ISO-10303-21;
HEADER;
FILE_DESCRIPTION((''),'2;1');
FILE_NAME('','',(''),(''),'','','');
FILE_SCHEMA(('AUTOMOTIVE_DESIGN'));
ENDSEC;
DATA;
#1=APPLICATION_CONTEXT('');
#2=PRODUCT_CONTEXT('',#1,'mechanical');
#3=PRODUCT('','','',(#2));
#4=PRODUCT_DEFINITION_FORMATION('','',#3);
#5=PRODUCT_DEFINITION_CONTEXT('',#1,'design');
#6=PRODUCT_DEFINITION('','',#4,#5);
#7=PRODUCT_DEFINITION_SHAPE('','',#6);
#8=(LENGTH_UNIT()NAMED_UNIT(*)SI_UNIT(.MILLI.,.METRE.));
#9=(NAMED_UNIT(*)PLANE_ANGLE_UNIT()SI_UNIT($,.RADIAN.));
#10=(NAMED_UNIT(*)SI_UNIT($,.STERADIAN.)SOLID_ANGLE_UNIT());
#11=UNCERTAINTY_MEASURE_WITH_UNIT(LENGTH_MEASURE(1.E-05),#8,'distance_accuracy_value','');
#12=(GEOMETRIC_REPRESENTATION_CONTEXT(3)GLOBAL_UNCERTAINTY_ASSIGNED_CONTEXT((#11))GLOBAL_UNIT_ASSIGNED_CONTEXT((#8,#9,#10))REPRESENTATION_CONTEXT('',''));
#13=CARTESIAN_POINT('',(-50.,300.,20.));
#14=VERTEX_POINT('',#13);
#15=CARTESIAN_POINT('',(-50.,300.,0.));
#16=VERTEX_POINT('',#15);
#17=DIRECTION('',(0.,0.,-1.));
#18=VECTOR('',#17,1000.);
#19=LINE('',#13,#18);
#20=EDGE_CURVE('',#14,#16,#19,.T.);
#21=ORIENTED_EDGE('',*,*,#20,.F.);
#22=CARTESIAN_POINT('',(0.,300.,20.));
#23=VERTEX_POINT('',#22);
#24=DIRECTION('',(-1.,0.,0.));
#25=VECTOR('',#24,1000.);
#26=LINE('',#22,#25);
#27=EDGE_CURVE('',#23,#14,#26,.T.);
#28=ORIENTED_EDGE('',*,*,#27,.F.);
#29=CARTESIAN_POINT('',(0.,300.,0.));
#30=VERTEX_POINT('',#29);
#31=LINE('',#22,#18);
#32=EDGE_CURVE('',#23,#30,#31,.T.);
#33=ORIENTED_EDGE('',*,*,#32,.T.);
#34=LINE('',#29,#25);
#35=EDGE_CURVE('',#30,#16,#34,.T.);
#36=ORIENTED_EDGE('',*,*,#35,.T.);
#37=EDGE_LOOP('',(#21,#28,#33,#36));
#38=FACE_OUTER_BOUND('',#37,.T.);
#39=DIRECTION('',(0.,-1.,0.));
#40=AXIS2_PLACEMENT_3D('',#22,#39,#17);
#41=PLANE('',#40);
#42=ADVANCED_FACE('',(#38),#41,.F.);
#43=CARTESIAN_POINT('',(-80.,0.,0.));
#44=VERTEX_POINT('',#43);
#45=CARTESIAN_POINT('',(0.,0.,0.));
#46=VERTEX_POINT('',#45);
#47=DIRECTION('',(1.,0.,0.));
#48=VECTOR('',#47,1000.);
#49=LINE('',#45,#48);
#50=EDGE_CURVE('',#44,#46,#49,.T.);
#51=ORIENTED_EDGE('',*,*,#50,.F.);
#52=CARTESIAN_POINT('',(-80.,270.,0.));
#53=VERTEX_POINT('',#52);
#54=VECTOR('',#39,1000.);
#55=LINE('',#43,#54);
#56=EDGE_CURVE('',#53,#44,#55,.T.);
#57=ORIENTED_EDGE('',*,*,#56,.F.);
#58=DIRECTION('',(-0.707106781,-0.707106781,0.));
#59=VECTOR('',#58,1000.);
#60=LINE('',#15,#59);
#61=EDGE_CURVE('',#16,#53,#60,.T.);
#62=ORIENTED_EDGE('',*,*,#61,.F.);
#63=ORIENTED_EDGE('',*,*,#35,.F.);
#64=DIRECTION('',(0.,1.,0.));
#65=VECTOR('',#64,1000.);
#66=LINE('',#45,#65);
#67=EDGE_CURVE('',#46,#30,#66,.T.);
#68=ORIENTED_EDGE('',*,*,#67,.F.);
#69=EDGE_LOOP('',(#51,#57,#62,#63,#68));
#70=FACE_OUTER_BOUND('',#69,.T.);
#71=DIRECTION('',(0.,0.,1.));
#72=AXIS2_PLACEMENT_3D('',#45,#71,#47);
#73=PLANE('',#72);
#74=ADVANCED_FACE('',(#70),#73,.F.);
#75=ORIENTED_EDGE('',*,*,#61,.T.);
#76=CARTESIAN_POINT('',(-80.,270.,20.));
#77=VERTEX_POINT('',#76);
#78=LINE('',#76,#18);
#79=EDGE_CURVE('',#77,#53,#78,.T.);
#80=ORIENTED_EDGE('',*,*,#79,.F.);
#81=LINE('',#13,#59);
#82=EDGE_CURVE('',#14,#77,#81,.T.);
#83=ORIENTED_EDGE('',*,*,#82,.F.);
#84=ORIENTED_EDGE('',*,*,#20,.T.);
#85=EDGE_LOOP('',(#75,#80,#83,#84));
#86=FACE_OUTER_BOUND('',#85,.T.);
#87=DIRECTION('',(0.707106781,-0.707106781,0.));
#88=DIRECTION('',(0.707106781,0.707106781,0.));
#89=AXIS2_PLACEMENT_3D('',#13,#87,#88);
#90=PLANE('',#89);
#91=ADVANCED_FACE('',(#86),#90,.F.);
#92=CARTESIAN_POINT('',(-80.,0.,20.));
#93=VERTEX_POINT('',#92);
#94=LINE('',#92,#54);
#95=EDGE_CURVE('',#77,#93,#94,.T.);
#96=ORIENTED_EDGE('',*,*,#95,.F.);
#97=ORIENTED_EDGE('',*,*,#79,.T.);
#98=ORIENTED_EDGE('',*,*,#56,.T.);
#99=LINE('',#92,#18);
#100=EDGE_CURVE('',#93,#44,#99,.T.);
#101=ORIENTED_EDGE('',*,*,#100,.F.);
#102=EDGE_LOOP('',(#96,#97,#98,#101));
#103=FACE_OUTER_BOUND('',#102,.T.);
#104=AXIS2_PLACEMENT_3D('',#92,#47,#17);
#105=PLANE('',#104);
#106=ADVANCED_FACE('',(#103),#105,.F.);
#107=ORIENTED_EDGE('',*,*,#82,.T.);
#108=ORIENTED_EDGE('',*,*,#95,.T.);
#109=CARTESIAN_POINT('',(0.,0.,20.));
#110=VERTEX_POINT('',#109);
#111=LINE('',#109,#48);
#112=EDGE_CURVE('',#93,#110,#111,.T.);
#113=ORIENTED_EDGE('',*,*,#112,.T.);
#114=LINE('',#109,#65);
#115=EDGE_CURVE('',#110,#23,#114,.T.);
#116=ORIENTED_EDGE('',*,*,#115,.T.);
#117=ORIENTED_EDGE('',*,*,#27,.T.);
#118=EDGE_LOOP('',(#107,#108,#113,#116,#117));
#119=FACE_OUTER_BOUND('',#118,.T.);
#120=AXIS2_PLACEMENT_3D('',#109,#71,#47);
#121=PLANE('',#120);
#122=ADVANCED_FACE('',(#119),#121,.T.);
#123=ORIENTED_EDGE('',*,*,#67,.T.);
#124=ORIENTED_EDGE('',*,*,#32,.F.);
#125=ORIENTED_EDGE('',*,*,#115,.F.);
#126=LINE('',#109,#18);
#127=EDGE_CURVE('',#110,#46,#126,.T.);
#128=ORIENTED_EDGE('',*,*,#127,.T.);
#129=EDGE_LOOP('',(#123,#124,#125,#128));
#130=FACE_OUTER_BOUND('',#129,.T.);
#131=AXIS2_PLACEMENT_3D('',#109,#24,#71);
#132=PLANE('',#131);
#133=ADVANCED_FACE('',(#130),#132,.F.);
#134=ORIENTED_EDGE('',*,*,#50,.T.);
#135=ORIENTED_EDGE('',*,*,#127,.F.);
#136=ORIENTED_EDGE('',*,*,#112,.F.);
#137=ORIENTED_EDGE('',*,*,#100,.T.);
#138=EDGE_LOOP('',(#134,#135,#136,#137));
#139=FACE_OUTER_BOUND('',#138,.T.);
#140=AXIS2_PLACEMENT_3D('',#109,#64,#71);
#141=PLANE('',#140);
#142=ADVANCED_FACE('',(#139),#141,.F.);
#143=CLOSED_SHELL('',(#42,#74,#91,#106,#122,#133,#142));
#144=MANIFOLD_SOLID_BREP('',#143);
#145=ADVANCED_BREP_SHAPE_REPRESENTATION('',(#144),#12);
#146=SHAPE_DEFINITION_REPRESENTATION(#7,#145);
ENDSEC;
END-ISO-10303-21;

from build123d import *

# Parameters (mm, degrees)
BOSS_EXTRUDE1_DEPTH = 20


with BuildPart() as part:
    # Sketch1 → Boss-Extrude1 (new body)
    with BuildSketch(Plane.XY):
        Polygon((-50, 300), (-80, 270), (-80, 0), (0, 0), (0, 300), align=None)
    extrude(amount=BOSS_EXTRUDE1_DEPTH)


solid = part.part
